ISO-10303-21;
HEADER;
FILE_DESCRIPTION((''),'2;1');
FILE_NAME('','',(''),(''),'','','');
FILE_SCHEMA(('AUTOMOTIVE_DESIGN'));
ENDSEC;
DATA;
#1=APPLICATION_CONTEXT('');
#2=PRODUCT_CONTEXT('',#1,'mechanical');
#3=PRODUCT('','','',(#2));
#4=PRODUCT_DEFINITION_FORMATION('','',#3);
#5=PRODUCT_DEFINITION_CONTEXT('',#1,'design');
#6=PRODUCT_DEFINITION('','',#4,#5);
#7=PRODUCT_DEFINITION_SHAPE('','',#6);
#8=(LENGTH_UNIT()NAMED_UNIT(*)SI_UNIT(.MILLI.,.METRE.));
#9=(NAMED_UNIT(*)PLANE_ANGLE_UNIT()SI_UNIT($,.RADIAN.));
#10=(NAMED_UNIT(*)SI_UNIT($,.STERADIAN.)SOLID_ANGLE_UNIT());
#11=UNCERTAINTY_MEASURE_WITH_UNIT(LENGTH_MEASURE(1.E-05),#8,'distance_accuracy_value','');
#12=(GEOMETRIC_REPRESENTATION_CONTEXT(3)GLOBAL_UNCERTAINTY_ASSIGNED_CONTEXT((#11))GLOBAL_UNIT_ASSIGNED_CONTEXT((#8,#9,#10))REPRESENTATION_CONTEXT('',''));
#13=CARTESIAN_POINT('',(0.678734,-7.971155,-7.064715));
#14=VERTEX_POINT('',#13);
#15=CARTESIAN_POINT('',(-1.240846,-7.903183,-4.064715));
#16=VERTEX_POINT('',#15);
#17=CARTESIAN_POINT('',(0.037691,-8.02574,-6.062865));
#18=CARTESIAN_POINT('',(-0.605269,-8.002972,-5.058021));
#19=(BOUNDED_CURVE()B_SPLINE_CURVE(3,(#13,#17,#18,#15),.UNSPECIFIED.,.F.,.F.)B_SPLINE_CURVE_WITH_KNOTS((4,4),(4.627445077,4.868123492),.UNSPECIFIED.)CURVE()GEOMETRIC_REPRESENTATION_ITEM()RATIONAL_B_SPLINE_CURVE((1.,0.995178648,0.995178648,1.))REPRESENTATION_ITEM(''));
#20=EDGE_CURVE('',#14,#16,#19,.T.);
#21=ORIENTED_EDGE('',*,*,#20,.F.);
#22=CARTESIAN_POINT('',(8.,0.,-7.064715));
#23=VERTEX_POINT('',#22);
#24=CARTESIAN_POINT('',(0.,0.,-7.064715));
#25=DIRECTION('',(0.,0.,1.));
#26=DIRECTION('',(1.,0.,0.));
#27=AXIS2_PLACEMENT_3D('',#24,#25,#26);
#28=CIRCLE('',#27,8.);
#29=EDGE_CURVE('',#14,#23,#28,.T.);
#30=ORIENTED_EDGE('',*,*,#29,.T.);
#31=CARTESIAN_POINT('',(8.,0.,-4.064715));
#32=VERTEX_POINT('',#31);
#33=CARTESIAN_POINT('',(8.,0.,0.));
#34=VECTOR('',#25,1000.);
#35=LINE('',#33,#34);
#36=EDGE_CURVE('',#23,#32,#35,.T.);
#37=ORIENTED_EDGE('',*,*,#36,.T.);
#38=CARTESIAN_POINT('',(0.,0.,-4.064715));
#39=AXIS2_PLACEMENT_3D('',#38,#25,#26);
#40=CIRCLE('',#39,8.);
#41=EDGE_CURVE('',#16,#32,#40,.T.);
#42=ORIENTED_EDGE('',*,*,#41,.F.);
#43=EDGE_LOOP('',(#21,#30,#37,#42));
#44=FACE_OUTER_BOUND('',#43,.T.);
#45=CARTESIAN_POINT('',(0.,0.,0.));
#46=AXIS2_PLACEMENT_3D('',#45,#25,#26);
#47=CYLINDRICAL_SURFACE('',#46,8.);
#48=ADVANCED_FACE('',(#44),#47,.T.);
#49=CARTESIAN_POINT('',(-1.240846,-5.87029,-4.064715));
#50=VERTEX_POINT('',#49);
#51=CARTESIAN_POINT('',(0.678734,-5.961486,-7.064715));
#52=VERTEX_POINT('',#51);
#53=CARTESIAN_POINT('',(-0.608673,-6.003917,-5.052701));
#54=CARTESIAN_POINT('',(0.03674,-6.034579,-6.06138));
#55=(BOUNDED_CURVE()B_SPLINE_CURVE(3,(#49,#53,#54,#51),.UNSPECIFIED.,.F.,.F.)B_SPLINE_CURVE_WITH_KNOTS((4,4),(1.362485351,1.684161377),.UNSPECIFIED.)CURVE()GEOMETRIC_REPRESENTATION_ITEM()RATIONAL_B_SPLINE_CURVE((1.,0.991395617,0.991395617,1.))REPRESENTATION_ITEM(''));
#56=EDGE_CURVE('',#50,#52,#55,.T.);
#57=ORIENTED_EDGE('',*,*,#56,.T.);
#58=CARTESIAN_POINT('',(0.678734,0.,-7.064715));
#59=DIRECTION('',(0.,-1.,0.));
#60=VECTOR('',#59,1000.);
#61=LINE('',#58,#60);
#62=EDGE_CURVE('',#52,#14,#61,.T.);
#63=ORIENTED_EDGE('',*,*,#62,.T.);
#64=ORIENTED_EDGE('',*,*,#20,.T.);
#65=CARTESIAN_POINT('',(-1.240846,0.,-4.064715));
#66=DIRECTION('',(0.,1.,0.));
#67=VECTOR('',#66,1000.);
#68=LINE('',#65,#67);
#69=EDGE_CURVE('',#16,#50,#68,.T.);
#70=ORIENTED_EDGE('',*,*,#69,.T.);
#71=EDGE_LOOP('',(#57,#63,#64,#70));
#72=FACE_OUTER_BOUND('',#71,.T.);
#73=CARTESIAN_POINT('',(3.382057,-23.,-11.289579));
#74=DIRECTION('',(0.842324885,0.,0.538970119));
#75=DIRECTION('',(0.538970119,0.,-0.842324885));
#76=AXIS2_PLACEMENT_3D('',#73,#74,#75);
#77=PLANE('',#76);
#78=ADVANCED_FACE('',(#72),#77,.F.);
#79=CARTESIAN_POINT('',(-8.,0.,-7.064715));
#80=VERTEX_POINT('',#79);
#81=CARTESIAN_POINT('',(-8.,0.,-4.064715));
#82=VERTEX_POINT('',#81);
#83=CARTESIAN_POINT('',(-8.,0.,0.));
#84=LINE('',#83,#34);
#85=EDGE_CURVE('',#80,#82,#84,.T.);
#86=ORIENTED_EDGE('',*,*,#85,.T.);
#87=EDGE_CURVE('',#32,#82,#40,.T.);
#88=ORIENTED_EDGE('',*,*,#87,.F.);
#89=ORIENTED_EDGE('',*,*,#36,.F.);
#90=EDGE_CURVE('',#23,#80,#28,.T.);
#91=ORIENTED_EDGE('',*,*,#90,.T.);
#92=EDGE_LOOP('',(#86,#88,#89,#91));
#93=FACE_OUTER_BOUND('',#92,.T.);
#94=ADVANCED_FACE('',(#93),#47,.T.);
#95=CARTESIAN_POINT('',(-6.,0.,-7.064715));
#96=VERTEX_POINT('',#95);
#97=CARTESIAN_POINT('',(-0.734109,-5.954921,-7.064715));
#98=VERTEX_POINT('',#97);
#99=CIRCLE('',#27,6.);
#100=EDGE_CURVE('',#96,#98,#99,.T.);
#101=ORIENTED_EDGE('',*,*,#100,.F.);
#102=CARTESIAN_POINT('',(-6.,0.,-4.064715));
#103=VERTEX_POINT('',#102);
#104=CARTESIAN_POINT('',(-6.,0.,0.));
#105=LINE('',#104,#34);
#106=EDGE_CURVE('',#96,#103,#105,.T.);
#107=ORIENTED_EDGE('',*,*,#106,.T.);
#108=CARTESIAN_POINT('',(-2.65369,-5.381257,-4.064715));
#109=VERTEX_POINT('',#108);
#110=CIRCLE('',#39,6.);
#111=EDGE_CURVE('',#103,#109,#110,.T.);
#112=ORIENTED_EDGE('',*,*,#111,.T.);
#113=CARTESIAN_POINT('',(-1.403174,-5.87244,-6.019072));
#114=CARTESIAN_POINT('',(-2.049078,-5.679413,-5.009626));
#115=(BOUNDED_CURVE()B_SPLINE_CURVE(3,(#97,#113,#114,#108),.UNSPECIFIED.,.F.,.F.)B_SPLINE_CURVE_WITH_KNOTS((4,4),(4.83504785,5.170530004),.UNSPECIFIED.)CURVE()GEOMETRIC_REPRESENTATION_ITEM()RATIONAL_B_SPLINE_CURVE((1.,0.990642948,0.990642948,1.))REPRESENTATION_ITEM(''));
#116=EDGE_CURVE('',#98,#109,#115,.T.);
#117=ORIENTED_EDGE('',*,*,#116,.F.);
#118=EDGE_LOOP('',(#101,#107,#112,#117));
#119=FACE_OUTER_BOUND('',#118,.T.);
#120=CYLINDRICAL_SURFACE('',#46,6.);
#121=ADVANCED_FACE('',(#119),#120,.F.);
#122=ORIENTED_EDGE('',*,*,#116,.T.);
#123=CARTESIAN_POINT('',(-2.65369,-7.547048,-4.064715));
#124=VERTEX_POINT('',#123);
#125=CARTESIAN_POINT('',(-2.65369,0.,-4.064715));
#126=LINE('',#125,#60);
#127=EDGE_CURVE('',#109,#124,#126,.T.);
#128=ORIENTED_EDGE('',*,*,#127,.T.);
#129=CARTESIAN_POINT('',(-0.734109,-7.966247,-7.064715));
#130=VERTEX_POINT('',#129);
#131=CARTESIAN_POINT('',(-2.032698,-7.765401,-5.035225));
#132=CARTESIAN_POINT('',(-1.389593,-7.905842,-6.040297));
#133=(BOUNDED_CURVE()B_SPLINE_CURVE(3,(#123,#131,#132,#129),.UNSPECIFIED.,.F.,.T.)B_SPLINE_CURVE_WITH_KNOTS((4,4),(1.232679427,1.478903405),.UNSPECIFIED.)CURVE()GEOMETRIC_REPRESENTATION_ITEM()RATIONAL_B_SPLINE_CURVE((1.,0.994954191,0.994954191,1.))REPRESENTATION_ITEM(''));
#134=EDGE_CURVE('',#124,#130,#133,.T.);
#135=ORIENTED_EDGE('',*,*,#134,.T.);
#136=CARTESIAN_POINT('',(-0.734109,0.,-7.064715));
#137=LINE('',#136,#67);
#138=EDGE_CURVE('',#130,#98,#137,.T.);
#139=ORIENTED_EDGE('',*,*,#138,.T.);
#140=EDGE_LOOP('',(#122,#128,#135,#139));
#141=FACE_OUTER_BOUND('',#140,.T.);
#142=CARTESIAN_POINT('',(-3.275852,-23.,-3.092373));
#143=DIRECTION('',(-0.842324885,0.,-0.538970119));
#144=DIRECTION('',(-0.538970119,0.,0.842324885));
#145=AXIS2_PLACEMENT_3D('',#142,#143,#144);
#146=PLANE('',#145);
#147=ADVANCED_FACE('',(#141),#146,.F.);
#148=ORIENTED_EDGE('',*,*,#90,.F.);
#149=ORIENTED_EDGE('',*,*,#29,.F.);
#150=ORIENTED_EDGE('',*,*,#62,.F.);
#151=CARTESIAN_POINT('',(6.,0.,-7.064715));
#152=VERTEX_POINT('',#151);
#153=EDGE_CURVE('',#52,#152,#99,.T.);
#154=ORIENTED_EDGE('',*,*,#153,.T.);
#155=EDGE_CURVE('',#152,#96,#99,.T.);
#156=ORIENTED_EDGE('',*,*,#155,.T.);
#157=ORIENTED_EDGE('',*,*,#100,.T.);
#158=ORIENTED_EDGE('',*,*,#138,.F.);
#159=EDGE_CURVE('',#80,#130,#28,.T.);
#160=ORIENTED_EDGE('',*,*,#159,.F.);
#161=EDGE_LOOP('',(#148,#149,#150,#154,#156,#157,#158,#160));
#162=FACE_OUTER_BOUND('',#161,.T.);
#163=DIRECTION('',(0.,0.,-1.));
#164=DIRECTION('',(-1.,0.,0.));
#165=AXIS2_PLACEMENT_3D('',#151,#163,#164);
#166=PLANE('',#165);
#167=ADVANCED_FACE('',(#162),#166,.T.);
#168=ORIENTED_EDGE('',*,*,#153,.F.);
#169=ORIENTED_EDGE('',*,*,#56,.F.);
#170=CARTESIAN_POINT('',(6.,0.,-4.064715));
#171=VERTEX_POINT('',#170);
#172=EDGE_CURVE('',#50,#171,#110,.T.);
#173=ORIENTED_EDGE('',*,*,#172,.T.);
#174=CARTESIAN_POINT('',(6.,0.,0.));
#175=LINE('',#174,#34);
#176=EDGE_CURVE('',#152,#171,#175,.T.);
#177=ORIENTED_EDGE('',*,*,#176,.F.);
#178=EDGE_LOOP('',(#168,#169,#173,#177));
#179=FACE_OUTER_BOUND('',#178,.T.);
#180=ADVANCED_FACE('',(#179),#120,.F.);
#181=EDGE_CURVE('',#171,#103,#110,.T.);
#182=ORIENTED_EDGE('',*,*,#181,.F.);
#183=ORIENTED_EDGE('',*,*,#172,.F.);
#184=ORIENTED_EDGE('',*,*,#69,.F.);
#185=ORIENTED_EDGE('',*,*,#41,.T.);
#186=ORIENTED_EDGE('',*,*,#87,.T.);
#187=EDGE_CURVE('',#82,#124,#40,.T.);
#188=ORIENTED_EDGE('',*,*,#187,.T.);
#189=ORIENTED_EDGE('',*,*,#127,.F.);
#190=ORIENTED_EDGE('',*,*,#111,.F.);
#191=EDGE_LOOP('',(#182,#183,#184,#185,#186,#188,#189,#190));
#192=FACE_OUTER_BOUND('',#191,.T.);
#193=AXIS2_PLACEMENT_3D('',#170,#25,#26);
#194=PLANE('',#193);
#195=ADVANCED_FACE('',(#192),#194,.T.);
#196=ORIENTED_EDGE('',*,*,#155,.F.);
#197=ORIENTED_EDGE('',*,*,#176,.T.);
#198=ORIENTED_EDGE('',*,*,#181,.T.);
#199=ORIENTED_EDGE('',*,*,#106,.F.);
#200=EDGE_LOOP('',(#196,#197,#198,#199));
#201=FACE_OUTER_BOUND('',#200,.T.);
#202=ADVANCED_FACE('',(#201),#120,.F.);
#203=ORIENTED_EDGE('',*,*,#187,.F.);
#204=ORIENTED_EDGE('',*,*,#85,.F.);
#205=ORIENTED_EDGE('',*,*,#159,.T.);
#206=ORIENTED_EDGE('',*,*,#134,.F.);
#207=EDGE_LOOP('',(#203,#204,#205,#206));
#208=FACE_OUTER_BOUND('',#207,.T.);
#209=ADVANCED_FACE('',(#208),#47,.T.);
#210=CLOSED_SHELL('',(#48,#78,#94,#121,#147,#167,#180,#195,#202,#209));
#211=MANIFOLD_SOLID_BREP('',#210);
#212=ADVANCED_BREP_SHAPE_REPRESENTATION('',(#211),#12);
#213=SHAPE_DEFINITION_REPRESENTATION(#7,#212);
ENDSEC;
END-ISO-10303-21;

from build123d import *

# Parameters (mm, degrees)
SKETCH1_W          = 2
SKETCH1_H          = 3
CUT_EXTRUDE1_DEPTH = 23


with BuildPart() as part:
    # Sketch1 → Revolve1 (revolve)
    with BuildSketch(Plane(origin=(0, 0, 0), x_dir=(1, 0, 0), z_dir=(0, 1, 0))):
        with Locations((7, 5.564714504)):
            Rectangle(SKETCH1_W, SKETCH1_H)
    revolve(axis=Axis((0, 0, 0), (0, 0, -1)))

    # Sketch2 → Cut-Extrude1 (cut)
    with BuildSketch(Plane(origin=(0, 0, 0), x_dir=(1, 0, 0), z_dir=(0, 1, 0))):
        Polygon((-3.27585187, 3.09237347), (2.379628245, 11.930992665), (3.38205654, 11.289578756), (-2.273423575, 2.450959561), align=None)
    extrude(amount=-CUT_EXTRUDE1_DEPTH, mode=Mode.SUBTRACT)


solid = part.part
